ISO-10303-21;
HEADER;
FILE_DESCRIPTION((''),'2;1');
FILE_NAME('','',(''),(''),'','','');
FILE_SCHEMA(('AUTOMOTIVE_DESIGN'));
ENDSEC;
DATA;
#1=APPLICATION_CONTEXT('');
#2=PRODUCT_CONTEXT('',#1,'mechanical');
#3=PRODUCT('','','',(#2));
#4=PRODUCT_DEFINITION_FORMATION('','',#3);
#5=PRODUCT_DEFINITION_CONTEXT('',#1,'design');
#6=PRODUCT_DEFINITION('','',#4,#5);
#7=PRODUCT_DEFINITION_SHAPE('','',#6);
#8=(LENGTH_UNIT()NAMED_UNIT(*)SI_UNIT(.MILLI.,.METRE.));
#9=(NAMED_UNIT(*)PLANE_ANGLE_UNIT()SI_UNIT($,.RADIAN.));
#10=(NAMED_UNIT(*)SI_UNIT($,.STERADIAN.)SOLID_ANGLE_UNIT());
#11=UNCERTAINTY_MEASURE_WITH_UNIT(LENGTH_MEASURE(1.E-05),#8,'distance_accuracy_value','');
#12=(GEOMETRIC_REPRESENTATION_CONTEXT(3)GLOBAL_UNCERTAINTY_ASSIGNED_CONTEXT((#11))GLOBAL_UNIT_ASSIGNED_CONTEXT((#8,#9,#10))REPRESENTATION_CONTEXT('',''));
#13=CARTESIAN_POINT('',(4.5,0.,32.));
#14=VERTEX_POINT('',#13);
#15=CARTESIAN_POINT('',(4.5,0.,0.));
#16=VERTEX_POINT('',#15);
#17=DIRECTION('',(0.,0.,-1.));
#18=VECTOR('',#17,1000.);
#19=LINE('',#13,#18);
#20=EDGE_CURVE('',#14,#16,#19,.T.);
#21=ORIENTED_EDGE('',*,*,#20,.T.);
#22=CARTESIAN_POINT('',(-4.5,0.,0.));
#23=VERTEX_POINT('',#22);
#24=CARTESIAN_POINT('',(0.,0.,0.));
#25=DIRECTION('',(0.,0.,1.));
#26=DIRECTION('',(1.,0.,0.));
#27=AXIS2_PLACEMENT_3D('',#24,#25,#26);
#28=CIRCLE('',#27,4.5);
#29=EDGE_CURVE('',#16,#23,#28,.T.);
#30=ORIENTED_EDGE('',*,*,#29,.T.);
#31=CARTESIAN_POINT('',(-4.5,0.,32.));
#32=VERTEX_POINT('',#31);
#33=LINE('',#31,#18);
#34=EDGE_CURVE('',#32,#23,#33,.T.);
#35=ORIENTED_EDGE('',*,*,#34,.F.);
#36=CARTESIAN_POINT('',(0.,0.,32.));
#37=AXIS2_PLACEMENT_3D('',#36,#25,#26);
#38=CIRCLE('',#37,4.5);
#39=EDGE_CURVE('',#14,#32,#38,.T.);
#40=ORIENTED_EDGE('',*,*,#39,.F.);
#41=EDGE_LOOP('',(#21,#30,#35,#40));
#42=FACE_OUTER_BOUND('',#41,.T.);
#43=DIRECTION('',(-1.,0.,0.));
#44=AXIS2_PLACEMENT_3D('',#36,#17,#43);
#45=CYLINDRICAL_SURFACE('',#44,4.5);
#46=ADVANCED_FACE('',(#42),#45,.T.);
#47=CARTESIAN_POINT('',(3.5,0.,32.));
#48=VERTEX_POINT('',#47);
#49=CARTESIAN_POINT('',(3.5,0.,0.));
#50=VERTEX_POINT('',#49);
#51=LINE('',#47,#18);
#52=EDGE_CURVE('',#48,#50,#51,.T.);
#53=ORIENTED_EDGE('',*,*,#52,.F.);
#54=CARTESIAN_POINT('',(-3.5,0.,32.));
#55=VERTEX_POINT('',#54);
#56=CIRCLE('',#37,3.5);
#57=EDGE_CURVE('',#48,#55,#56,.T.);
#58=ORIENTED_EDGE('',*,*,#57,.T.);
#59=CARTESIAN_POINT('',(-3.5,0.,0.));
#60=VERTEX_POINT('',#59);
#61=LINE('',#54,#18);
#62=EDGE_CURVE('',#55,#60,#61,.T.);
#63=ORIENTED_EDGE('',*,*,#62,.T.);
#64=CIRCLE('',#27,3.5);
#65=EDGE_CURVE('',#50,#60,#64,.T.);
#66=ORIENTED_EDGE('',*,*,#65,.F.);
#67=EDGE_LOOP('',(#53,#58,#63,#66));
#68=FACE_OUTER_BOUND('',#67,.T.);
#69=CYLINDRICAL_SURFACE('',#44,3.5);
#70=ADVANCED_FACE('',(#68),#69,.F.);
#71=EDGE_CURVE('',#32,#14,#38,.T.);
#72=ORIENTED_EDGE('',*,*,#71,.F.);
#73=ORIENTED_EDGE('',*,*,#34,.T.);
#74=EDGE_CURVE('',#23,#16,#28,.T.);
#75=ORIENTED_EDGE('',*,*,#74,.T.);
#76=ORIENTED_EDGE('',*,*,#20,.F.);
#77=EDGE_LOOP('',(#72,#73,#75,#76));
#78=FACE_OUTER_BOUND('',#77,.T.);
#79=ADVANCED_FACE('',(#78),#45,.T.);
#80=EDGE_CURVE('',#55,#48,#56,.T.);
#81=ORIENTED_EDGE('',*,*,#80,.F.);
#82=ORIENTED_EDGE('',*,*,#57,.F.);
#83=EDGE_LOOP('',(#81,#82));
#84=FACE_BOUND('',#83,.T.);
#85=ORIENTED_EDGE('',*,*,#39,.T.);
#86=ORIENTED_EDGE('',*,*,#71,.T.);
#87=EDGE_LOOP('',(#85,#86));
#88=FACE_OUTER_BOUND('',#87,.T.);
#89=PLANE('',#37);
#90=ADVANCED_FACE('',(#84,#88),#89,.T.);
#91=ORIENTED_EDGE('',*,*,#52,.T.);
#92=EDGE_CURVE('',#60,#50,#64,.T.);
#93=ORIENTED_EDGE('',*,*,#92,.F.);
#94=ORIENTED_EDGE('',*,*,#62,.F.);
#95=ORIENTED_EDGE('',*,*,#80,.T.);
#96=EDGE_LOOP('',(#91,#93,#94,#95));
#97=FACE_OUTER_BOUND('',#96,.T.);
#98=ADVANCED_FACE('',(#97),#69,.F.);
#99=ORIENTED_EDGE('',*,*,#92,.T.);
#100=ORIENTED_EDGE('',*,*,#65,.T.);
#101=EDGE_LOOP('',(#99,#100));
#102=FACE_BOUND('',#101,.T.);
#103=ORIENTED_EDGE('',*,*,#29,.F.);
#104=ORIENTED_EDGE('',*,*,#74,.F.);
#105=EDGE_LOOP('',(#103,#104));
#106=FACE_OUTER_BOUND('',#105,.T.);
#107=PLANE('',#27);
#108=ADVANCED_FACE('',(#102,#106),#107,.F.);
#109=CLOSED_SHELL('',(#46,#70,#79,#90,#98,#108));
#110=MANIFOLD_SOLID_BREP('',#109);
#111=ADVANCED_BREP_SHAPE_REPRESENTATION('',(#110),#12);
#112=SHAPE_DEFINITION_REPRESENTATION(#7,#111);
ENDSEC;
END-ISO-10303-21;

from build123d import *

# Parameters (mm, degrees)
SKETCH1_R           = 4.5
SKETCH1_R_2         = 3.5
BOSS_EXTRUDE1_DEPTH = 32


with BuildPart() as part:
    # Sketch1 → Boss-Extrude1 (new body)
    with BuildSketch(Plane.XY):
        Circle(SKETCH1_R)
        Circle(SKETCH1_R_2, mode=Mode.SUBTRACT)
    extrude(amount=BOSS_EXTRUDE1_DEPTH)


solid = part.part
